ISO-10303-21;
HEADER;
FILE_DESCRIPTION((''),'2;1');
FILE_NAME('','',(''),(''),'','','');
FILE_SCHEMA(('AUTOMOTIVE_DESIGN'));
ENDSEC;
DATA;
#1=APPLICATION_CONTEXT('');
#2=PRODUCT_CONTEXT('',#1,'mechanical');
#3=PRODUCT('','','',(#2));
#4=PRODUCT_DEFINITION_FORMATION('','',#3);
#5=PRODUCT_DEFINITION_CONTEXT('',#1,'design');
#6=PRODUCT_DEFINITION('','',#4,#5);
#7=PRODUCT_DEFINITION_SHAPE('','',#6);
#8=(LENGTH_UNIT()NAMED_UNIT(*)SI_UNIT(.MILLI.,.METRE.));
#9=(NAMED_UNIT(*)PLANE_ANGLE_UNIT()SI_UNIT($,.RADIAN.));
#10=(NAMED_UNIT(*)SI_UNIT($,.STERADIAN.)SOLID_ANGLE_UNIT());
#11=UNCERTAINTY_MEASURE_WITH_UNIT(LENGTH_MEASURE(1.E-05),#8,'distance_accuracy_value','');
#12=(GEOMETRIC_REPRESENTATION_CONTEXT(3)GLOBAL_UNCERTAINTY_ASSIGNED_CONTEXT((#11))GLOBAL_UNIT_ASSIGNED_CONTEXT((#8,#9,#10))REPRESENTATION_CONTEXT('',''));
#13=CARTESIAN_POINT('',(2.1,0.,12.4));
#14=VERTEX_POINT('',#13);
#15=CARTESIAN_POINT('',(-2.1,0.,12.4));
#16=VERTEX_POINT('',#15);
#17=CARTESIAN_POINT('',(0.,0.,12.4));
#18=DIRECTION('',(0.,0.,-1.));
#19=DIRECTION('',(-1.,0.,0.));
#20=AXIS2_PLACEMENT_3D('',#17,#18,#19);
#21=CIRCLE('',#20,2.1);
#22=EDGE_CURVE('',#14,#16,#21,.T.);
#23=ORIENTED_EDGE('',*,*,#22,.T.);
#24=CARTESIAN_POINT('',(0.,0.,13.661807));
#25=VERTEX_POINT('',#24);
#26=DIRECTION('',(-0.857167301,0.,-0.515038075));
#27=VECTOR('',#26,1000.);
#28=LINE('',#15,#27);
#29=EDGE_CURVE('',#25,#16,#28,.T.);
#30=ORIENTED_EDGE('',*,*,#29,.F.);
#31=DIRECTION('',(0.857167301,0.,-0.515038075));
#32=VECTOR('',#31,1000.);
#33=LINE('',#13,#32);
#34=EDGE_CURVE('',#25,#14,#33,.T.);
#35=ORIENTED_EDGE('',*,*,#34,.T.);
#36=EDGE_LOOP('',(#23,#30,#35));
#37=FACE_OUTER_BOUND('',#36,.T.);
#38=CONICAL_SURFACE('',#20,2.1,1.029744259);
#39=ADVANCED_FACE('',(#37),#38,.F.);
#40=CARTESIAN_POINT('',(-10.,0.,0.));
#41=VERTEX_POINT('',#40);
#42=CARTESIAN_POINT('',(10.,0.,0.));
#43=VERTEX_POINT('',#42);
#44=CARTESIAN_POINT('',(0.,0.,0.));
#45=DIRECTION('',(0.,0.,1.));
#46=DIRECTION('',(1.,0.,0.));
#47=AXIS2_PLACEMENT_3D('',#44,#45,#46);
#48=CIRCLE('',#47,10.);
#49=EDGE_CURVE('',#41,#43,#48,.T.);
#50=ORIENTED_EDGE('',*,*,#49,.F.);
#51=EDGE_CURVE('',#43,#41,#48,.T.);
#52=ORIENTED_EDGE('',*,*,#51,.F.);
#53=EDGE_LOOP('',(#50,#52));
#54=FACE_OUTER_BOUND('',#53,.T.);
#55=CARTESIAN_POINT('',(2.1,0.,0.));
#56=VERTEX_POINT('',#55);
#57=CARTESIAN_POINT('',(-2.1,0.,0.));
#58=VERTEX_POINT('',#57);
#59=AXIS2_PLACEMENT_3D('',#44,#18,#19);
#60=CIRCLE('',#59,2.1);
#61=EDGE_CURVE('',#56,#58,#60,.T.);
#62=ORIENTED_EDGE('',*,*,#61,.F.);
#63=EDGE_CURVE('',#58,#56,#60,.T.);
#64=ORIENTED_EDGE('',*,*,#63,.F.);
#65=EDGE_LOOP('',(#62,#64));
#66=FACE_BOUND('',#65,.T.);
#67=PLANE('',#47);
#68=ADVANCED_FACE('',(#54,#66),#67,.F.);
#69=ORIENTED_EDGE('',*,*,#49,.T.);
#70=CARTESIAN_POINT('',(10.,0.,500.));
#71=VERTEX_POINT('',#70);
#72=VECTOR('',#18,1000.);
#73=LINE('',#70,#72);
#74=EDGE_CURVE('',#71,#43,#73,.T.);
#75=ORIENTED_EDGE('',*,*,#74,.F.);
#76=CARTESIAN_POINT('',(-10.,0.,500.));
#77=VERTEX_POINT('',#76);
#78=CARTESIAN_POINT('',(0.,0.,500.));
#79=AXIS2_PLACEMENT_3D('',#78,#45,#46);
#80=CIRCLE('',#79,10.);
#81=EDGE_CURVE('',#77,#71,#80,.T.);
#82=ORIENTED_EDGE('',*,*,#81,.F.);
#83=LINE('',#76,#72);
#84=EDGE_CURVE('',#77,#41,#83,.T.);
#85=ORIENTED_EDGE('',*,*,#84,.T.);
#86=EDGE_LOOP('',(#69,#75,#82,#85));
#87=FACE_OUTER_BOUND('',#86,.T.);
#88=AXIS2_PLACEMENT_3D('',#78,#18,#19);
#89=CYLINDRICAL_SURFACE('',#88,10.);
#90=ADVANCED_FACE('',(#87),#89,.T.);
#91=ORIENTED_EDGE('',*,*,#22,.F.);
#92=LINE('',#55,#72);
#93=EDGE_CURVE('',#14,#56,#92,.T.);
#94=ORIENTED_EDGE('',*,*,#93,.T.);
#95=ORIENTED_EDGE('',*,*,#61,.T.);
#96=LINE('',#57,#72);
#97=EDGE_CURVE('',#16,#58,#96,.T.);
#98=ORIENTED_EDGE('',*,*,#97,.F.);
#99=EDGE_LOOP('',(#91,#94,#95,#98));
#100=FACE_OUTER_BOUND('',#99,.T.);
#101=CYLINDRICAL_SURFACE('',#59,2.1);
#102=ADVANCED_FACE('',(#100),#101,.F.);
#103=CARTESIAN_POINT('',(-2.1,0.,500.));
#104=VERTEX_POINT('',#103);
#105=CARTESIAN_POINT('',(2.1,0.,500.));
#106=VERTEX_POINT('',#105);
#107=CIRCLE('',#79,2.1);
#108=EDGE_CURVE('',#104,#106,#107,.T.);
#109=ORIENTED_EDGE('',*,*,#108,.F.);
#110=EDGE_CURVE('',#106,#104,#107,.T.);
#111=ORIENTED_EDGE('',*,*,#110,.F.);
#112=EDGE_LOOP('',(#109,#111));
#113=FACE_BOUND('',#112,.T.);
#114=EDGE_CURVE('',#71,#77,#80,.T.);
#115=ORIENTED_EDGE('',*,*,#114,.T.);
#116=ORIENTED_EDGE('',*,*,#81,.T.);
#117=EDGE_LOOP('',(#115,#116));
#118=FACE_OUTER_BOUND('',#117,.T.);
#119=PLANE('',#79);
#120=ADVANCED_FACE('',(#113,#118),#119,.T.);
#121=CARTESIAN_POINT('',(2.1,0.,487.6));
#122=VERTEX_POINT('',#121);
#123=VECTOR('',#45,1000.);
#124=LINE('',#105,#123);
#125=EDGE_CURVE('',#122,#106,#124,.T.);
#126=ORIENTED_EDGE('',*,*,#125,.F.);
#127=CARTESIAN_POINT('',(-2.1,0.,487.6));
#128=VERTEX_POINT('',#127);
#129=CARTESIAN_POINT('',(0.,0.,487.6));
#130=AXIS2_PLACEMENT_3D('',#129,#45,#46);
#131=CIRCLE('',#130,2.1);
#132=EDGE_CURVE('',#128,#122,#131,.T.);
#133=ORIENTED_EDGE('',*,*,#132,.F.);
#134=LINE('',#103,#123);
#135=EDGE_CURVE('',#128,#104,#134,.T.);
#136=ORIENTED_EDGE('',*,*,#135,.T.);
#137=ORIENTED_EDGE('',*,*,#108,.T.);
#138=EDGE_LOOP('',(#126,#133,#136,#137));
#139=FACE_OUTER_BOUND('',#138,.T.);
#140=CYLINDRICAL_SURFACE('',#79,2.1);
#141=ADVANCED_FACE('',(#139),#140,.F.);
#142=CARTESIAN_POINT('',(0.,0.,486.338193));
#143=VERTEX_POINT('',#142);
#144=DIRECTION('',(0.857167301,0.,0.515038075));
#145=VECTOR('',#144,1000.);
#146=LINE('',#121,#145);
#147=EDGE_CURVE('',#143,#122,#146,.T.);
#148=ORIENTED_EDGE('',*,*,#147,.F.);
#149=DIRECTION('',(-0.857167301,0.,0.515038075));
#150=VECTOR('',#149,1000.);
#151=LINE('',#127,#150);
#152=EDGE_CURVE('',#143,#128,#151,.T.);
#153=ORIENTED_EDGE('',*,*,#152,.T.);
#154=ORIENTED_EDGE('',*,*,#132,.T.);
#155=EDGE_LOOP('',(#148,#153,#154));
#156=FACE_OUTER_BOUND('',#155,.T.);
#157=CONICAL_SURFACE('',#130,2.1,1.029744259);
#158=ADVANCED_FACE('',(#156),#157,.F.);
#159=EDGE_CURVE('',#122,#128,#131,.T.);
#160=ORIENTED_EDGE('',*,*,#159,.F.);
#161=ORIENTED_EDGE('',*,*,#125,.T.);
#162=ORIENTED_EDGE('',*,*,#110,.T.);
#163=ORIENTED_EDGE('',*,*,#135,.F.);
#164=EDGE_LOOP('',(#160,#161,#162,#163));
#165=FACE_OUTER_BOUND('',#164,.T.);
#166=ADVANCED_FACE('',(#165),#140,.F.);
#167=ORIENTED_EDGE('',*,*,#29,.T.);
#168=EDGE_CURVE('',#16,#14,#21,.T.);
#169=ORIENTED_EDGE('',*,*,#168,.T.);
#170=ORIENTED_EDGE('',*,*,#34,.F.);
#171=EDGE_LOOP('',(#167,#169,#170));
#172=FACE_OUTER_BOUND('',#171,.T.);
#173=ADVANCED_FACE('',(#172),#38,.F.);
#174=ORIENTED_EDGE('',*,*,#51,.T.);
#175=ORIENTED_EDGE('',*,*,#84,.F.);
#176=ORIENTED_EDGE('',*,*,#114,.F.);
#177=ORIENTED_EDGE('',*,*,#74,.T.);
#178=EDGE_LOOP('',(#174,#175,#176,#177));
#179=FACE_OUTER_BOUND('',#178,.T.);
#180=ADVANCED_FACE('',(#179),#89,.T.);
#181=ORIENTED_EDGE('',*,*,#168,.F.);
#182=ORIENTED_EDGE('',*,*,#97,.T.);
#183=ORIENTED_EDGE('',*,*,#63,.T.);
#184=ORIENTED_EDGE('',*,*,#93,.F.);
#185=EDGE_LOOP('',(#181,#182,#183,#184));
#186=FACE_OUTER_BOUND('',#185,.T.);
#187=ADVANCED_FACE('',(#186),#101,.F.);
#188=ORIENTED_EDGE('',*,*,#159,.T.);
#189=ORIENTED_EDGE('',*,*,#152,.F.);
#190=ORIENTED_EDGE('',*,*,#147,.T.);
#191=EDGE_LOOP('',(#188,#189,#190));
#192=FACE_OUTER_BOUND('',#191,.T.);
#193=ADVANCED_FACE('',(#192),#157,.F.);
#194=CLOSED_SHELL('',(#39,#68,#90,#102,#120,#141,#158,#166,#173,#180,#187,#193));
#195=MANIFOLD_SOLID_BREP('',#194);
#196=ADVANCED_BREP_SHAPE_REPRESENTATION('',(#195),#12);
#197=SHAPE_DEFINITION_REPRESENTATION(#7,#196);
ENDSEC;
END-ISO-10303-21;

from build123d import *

# Parameters (mm, degrees)
SKETCH_1_R             = 10
EXTRUDE_1_DEPTH        = 500
HOLE_WIZARD_M5_1_D     = 4.2
HOLE_WIZARD_M5_1_DEPTH = 12.4
HOLE_WIZARD_M5_1_TIP   = 1.2618073
HOLE_WIZARD_M5_2_D     = 4.2
HOLE_WIZARD_M5_2_DEPTH = 12.4
HOLE_WIZARD_M5_2_TIP   = 1.2618073


with BuildPart() as part:
    # 草图1 → 凸台-拉伸1 (new body)
    with BuildSketch(Plane.XY):
        Circle(SKETCH_1_R)
    extrude(amount=EXTRUDE_1_DEPTH)

    # M5 螺纹孔1
    with Locations(Plane(origin=(0, 0, 0), x_dir=(-1, 0, 0), z_dir=(0, 0, -1))):
        with Locations((0, 0)):
            Hole(HOLE_WIZARD_M5_1_D / 2, depth=HOLE_WIZARD_M5_1_DEPTH)
            with Locations((0, 0, -(HOLE_WIZARD_M5_1_DEPTH + HOLE_WIZARD_M5_1_TIP / 2))):  # 118° drill point
                Cone(0, HOLE_WIZARD_M5_1_D / 2, HOLE_WIZARD_M5_1_TIP, mode=Mode.SUBTRACT)

    # M5 螺纹孔2
    with Locations(Plane.XY.offset(500)):
        with Locations((0, 0)):
            Hole(HOLE_WIZARD_M5_2_D / 2, depth=HOLE_WIZARD_M5_2_DEPTH)
            with Locations((0, 0, -(HOLE_WIZARD_M5_2_DEPTH + HOLE_WIZARD_M5_2_TIP / 2))):  # 118° drill point
                Cone(0, HOLE_WIZARD_M5_2_D / 2, HOLE_WIZARD_M5_2_TIP, mode=Mode.SUBTRACT)


solid = part.part
